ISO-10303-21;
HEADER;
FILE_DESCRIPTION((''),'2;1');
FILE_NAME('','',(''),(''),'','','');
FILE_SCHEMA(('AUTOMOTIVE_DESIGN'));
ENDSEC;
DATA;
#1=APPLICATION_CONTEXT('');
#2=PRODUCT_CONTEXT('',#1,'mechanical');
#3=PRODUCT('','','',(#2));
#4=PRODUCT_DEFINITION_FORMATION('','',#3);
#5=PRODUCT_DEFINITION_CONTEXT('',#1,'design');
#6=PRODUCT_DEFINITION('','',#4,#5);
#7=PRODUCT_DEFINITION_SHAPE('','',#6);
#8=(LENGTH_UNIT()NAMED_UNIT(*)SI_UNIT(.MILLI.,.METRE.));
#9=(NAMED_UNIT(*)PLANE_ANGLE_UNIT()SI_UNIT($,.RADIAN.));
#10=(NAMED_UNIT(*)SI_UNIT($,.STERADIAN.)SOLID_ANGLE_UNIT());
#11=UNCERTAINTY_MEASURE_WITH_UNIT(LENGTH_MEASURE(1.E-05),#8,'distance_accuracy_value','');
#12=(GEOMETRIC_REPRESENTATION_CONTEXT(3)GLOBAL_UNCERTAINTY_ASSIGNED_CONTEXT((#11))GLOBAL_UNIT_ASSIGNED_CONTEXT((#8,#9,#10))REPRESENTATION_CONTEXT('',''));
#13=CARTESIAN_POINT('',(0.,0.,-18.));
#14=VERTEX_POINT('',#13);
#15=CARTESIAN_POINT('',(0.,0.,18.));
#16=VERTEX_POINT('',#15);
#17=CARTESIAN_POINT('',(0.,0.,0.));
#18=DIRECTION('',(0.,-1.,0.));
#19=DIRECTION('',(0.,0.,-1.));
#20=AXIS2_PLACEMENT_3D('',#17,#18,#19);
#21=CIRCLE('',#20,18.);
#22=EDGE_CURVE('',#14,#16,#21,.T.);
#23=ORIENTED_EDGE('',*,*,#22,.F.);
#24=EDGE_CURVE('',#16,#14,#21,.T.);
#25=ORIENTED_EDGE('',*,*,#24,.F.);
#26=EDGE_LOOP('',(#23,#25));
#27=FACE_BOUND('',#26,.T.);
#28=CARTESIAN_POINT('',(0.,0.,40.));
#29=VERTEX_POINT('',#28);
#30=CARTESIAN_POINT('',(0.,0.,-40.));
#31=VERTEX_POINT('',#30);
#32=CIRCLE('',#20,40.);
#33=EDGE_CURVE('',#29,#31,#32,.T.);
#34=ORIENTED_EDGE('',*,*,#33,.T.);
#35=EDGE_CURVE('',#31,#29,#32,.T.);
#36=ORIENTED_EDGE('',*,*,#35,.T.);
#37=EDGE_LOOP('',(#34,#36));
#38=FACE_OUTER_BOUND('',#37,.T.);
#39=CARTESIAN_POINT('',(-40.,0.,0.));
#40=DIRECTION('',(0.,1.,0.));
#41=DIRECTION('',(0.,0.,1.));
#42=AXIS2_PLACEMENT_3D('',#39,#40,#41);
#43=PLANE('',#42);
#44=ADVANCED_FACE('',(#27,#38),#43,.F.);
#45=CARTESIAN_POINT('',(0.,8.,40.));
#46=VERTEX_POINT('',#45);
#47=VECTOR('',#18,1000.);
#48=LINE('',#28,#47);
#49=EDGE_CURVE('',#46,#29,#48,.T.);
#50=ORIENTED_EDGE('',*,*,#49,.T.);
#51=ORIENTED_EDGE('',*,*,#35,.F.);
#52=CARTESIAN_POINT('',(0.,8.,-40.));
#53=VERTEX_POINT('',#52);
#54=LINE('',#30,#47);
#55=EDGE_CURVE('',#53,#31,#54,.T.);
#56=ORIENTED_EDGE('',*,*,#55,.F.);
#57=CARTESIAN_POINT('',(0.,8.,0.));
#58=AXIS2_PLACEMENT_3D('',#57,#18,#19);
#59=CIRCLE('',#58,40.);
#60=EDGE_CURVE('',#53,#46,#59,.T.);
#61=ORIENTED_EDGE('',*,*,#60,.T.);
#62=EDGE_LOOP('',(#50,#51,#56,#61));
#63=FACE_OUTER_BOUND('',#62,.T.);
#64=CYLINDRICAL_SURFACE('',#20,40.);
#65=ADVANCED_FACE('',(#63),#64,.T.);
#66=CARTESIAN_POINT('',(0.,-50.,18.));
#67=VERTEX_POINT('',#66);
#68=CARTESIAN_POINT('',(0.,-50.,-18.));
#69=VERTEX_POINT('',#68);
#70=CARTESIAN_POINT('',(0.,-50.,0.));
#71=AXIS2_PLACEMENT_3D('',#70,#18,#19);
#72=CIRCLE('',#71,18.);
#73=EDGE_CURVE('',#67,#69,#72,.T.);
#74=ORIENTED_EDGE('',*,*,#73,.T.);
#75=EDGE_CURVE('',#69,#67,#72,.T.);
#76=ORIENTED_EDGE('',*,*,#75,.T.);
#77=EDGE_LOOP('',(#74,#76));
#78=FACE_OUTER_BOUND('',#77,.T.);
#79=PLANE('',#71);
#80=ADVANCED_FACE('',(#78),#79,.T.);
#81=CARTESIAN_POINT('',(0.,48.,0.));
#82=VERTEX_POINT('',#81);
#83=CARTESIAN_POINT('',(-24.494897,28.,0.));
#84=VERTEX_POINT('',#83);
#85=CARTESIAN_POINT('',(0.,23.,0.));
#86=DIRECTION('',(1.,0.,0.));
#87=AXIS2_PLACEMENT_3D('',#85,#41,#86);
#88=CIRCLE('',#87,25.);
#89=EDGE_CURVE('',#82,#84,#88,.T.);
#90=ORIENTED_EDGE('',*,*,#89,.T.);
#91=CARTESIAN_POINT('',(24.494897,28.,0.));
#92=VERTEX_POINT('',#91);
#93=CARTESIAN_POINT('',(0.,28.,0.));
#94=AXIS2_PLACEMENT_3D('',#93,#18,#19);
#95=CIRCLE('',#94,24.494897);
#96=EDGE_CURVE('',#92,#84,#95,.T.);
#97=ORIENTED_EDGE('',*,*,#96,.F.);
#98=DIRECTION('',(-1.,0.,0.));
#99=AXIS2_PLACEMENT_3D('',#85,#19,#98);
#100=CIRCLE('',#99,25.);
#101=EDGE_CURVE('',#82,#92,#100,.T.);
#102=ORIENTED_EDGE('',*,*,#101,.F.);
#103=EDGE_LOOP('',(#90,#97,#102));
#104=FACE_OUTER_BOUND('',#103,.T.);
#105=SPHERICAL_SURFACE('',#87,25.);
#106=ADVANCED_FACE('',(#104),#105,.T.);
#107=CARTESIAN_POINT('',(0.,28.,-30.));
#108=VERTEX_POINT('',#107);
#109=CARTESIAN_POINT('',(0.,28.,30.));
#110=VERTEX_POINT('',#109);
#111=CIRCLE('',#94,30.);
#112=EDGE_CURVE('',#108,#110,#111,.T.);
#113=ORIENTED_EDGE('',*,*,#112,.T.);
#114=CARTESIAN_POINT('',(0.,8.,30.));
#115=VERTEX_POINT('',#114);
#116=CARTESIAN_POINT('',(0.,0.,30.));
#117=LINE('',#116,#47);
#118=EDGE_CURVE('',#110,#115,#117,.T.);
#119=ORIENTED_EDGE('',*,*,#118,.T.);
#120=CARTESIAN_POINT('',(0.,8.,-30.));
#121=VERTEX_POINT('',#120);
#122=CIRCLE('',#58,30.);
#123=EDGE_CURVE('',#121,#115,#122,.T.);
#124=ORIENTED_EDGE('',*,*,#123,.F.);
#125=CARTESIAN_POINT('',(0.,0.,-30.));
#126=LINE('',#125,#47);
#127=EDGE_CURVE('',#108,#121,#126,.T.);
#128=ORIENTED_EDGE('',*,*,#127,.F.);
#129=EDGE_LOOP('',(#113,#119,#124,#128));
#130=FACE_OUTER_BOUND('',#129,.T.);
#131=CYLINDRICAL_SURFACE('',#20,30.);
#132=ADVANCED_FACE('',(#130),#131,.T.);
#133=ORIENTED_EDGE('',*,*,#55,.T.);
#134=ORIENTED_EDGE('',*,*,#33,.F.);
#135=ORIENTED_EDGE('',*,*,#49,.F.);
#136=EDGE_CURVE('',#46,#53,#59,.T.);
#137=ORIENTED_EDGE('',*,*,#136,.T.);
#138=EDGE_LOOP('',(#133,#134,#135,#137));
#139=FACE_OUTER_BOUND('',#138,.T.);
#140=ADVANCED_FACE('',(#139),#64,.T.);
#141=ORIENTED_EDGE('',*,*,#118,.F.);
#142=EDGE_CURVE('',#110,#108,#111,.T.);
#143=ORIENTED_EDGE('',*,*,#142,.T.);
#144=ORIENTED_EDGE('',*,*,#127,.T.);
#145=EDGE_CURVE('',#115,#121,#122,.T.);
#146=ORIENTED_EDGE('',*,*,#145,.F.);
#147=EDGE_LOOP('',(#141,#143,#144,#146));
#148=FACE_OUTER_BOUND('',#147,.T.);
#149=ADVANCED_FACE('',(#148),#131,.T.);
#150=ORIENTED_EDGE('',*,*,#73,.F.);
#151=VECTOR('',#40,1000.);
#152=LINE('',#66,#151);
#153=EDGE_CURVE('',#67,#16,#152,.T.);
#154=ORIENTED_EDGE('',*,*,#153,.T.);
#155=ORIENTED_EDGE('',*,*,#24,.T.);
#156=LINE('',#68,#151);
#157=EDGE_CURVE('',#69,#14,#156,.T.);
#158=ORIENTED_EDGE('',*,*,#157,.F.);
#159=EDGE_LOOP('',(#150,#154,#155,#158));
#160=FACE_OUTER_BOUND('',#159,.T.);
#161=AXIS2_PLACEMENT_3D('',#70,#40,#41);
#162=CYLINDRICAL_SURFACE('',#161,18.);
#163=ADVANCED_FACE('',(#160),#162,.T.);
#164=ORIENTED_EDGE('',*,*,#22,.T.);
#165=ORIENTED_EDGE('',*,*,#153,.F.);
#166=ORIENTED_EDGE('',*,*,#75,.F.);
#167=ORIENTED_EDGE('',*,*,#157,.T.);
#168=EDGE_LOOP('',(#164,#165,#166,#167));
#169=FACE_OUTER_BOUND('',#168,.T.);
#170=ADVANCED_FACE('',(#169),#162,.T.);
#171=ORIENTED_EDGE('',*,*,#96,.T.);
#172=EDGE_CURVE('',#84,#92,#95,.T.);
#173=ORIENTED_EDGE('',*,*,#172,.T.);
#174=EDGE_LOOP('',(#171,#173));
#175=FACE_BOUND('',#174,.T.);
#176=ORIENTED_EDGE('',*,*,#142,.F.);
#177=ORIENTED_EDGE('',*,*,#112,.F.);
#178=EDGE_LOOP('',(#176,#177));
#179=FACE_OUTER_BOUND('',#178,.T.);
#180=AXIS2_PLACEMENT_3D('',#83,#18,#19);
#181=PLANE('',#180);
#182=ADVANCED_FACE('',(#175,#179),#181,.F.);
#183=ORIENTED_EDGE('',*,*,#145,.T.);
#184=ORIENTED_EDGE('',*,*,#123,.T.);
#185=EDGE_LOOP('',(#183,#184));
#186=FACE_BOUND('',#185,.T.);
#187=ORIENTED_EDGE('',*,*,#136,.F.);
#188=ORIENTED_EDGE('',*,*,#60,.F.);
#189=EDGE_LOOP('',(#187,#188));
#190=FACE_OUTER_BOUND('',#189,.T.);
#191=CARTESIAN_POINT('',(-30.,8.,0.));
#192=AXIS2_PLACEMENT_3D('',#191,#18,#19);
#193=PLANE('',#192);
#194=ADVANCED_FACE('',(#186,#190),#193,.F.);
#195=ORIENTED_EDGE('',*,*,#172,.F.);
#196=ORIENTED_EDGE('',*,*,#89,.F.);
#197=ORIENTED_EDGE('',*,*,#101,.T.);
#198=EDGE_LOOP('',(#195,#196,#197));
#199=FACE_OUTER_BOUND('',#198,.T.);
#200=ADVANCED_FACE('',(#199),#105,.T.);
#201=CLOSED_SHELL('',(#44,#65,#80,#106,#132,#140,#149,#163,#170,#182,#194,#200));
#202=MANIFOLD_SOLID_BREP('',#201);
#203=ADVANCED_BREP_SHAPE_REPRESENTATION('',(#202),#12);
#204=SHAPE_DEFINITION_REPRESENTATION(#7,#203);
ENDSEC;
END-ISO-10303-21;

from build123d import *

# Parameters (mm, degrees)
SKETCH2_R           = 18
BOSS_EXTRUDE1_DEPTH = 50


with BuildPart() as part:
    # Sketch1 → Revolve1 (revolve)
    with BuildSketch(Plane.XY, mode=Mode.PRIVATE) as revolve1_sk:
        with BuildLine():
            Line((-24.494897428, 28), (-30, 28))
            Line((-30, 28), (-30, 8))
            Line((-30, 8), (-40, 8))
            Line((-40, 8), (-40, 0))
            Line((-40, 0), (0, 0))
            Line((0, 0), (0, 48))
            ThreePointArc((0, 48), (-15.811388301, 42.364916731), (-24.494897428, 28))
        make_face()
    revolve(revolve1_sk.sketch.rotate(Axis((0, 0, 0), (0, 1, 0)), 270), axis=Axis((0, 0, 0), (0, 1, 0)))

    # Sketch2 → Boss-Extrude1 (add)
    with BuildSketch(Plane(origin=(0, 0, 0), x_dir=(-1, 0, 0), z_dir=(0, -1, 0))):
        with Locations(Location((0, 0, 0), (0, 0, 90))):
            Circle(SKETCH2_R)
    extrude(amount=BOSS_EXTRUDE1_DEPTH)


solid = part.part
